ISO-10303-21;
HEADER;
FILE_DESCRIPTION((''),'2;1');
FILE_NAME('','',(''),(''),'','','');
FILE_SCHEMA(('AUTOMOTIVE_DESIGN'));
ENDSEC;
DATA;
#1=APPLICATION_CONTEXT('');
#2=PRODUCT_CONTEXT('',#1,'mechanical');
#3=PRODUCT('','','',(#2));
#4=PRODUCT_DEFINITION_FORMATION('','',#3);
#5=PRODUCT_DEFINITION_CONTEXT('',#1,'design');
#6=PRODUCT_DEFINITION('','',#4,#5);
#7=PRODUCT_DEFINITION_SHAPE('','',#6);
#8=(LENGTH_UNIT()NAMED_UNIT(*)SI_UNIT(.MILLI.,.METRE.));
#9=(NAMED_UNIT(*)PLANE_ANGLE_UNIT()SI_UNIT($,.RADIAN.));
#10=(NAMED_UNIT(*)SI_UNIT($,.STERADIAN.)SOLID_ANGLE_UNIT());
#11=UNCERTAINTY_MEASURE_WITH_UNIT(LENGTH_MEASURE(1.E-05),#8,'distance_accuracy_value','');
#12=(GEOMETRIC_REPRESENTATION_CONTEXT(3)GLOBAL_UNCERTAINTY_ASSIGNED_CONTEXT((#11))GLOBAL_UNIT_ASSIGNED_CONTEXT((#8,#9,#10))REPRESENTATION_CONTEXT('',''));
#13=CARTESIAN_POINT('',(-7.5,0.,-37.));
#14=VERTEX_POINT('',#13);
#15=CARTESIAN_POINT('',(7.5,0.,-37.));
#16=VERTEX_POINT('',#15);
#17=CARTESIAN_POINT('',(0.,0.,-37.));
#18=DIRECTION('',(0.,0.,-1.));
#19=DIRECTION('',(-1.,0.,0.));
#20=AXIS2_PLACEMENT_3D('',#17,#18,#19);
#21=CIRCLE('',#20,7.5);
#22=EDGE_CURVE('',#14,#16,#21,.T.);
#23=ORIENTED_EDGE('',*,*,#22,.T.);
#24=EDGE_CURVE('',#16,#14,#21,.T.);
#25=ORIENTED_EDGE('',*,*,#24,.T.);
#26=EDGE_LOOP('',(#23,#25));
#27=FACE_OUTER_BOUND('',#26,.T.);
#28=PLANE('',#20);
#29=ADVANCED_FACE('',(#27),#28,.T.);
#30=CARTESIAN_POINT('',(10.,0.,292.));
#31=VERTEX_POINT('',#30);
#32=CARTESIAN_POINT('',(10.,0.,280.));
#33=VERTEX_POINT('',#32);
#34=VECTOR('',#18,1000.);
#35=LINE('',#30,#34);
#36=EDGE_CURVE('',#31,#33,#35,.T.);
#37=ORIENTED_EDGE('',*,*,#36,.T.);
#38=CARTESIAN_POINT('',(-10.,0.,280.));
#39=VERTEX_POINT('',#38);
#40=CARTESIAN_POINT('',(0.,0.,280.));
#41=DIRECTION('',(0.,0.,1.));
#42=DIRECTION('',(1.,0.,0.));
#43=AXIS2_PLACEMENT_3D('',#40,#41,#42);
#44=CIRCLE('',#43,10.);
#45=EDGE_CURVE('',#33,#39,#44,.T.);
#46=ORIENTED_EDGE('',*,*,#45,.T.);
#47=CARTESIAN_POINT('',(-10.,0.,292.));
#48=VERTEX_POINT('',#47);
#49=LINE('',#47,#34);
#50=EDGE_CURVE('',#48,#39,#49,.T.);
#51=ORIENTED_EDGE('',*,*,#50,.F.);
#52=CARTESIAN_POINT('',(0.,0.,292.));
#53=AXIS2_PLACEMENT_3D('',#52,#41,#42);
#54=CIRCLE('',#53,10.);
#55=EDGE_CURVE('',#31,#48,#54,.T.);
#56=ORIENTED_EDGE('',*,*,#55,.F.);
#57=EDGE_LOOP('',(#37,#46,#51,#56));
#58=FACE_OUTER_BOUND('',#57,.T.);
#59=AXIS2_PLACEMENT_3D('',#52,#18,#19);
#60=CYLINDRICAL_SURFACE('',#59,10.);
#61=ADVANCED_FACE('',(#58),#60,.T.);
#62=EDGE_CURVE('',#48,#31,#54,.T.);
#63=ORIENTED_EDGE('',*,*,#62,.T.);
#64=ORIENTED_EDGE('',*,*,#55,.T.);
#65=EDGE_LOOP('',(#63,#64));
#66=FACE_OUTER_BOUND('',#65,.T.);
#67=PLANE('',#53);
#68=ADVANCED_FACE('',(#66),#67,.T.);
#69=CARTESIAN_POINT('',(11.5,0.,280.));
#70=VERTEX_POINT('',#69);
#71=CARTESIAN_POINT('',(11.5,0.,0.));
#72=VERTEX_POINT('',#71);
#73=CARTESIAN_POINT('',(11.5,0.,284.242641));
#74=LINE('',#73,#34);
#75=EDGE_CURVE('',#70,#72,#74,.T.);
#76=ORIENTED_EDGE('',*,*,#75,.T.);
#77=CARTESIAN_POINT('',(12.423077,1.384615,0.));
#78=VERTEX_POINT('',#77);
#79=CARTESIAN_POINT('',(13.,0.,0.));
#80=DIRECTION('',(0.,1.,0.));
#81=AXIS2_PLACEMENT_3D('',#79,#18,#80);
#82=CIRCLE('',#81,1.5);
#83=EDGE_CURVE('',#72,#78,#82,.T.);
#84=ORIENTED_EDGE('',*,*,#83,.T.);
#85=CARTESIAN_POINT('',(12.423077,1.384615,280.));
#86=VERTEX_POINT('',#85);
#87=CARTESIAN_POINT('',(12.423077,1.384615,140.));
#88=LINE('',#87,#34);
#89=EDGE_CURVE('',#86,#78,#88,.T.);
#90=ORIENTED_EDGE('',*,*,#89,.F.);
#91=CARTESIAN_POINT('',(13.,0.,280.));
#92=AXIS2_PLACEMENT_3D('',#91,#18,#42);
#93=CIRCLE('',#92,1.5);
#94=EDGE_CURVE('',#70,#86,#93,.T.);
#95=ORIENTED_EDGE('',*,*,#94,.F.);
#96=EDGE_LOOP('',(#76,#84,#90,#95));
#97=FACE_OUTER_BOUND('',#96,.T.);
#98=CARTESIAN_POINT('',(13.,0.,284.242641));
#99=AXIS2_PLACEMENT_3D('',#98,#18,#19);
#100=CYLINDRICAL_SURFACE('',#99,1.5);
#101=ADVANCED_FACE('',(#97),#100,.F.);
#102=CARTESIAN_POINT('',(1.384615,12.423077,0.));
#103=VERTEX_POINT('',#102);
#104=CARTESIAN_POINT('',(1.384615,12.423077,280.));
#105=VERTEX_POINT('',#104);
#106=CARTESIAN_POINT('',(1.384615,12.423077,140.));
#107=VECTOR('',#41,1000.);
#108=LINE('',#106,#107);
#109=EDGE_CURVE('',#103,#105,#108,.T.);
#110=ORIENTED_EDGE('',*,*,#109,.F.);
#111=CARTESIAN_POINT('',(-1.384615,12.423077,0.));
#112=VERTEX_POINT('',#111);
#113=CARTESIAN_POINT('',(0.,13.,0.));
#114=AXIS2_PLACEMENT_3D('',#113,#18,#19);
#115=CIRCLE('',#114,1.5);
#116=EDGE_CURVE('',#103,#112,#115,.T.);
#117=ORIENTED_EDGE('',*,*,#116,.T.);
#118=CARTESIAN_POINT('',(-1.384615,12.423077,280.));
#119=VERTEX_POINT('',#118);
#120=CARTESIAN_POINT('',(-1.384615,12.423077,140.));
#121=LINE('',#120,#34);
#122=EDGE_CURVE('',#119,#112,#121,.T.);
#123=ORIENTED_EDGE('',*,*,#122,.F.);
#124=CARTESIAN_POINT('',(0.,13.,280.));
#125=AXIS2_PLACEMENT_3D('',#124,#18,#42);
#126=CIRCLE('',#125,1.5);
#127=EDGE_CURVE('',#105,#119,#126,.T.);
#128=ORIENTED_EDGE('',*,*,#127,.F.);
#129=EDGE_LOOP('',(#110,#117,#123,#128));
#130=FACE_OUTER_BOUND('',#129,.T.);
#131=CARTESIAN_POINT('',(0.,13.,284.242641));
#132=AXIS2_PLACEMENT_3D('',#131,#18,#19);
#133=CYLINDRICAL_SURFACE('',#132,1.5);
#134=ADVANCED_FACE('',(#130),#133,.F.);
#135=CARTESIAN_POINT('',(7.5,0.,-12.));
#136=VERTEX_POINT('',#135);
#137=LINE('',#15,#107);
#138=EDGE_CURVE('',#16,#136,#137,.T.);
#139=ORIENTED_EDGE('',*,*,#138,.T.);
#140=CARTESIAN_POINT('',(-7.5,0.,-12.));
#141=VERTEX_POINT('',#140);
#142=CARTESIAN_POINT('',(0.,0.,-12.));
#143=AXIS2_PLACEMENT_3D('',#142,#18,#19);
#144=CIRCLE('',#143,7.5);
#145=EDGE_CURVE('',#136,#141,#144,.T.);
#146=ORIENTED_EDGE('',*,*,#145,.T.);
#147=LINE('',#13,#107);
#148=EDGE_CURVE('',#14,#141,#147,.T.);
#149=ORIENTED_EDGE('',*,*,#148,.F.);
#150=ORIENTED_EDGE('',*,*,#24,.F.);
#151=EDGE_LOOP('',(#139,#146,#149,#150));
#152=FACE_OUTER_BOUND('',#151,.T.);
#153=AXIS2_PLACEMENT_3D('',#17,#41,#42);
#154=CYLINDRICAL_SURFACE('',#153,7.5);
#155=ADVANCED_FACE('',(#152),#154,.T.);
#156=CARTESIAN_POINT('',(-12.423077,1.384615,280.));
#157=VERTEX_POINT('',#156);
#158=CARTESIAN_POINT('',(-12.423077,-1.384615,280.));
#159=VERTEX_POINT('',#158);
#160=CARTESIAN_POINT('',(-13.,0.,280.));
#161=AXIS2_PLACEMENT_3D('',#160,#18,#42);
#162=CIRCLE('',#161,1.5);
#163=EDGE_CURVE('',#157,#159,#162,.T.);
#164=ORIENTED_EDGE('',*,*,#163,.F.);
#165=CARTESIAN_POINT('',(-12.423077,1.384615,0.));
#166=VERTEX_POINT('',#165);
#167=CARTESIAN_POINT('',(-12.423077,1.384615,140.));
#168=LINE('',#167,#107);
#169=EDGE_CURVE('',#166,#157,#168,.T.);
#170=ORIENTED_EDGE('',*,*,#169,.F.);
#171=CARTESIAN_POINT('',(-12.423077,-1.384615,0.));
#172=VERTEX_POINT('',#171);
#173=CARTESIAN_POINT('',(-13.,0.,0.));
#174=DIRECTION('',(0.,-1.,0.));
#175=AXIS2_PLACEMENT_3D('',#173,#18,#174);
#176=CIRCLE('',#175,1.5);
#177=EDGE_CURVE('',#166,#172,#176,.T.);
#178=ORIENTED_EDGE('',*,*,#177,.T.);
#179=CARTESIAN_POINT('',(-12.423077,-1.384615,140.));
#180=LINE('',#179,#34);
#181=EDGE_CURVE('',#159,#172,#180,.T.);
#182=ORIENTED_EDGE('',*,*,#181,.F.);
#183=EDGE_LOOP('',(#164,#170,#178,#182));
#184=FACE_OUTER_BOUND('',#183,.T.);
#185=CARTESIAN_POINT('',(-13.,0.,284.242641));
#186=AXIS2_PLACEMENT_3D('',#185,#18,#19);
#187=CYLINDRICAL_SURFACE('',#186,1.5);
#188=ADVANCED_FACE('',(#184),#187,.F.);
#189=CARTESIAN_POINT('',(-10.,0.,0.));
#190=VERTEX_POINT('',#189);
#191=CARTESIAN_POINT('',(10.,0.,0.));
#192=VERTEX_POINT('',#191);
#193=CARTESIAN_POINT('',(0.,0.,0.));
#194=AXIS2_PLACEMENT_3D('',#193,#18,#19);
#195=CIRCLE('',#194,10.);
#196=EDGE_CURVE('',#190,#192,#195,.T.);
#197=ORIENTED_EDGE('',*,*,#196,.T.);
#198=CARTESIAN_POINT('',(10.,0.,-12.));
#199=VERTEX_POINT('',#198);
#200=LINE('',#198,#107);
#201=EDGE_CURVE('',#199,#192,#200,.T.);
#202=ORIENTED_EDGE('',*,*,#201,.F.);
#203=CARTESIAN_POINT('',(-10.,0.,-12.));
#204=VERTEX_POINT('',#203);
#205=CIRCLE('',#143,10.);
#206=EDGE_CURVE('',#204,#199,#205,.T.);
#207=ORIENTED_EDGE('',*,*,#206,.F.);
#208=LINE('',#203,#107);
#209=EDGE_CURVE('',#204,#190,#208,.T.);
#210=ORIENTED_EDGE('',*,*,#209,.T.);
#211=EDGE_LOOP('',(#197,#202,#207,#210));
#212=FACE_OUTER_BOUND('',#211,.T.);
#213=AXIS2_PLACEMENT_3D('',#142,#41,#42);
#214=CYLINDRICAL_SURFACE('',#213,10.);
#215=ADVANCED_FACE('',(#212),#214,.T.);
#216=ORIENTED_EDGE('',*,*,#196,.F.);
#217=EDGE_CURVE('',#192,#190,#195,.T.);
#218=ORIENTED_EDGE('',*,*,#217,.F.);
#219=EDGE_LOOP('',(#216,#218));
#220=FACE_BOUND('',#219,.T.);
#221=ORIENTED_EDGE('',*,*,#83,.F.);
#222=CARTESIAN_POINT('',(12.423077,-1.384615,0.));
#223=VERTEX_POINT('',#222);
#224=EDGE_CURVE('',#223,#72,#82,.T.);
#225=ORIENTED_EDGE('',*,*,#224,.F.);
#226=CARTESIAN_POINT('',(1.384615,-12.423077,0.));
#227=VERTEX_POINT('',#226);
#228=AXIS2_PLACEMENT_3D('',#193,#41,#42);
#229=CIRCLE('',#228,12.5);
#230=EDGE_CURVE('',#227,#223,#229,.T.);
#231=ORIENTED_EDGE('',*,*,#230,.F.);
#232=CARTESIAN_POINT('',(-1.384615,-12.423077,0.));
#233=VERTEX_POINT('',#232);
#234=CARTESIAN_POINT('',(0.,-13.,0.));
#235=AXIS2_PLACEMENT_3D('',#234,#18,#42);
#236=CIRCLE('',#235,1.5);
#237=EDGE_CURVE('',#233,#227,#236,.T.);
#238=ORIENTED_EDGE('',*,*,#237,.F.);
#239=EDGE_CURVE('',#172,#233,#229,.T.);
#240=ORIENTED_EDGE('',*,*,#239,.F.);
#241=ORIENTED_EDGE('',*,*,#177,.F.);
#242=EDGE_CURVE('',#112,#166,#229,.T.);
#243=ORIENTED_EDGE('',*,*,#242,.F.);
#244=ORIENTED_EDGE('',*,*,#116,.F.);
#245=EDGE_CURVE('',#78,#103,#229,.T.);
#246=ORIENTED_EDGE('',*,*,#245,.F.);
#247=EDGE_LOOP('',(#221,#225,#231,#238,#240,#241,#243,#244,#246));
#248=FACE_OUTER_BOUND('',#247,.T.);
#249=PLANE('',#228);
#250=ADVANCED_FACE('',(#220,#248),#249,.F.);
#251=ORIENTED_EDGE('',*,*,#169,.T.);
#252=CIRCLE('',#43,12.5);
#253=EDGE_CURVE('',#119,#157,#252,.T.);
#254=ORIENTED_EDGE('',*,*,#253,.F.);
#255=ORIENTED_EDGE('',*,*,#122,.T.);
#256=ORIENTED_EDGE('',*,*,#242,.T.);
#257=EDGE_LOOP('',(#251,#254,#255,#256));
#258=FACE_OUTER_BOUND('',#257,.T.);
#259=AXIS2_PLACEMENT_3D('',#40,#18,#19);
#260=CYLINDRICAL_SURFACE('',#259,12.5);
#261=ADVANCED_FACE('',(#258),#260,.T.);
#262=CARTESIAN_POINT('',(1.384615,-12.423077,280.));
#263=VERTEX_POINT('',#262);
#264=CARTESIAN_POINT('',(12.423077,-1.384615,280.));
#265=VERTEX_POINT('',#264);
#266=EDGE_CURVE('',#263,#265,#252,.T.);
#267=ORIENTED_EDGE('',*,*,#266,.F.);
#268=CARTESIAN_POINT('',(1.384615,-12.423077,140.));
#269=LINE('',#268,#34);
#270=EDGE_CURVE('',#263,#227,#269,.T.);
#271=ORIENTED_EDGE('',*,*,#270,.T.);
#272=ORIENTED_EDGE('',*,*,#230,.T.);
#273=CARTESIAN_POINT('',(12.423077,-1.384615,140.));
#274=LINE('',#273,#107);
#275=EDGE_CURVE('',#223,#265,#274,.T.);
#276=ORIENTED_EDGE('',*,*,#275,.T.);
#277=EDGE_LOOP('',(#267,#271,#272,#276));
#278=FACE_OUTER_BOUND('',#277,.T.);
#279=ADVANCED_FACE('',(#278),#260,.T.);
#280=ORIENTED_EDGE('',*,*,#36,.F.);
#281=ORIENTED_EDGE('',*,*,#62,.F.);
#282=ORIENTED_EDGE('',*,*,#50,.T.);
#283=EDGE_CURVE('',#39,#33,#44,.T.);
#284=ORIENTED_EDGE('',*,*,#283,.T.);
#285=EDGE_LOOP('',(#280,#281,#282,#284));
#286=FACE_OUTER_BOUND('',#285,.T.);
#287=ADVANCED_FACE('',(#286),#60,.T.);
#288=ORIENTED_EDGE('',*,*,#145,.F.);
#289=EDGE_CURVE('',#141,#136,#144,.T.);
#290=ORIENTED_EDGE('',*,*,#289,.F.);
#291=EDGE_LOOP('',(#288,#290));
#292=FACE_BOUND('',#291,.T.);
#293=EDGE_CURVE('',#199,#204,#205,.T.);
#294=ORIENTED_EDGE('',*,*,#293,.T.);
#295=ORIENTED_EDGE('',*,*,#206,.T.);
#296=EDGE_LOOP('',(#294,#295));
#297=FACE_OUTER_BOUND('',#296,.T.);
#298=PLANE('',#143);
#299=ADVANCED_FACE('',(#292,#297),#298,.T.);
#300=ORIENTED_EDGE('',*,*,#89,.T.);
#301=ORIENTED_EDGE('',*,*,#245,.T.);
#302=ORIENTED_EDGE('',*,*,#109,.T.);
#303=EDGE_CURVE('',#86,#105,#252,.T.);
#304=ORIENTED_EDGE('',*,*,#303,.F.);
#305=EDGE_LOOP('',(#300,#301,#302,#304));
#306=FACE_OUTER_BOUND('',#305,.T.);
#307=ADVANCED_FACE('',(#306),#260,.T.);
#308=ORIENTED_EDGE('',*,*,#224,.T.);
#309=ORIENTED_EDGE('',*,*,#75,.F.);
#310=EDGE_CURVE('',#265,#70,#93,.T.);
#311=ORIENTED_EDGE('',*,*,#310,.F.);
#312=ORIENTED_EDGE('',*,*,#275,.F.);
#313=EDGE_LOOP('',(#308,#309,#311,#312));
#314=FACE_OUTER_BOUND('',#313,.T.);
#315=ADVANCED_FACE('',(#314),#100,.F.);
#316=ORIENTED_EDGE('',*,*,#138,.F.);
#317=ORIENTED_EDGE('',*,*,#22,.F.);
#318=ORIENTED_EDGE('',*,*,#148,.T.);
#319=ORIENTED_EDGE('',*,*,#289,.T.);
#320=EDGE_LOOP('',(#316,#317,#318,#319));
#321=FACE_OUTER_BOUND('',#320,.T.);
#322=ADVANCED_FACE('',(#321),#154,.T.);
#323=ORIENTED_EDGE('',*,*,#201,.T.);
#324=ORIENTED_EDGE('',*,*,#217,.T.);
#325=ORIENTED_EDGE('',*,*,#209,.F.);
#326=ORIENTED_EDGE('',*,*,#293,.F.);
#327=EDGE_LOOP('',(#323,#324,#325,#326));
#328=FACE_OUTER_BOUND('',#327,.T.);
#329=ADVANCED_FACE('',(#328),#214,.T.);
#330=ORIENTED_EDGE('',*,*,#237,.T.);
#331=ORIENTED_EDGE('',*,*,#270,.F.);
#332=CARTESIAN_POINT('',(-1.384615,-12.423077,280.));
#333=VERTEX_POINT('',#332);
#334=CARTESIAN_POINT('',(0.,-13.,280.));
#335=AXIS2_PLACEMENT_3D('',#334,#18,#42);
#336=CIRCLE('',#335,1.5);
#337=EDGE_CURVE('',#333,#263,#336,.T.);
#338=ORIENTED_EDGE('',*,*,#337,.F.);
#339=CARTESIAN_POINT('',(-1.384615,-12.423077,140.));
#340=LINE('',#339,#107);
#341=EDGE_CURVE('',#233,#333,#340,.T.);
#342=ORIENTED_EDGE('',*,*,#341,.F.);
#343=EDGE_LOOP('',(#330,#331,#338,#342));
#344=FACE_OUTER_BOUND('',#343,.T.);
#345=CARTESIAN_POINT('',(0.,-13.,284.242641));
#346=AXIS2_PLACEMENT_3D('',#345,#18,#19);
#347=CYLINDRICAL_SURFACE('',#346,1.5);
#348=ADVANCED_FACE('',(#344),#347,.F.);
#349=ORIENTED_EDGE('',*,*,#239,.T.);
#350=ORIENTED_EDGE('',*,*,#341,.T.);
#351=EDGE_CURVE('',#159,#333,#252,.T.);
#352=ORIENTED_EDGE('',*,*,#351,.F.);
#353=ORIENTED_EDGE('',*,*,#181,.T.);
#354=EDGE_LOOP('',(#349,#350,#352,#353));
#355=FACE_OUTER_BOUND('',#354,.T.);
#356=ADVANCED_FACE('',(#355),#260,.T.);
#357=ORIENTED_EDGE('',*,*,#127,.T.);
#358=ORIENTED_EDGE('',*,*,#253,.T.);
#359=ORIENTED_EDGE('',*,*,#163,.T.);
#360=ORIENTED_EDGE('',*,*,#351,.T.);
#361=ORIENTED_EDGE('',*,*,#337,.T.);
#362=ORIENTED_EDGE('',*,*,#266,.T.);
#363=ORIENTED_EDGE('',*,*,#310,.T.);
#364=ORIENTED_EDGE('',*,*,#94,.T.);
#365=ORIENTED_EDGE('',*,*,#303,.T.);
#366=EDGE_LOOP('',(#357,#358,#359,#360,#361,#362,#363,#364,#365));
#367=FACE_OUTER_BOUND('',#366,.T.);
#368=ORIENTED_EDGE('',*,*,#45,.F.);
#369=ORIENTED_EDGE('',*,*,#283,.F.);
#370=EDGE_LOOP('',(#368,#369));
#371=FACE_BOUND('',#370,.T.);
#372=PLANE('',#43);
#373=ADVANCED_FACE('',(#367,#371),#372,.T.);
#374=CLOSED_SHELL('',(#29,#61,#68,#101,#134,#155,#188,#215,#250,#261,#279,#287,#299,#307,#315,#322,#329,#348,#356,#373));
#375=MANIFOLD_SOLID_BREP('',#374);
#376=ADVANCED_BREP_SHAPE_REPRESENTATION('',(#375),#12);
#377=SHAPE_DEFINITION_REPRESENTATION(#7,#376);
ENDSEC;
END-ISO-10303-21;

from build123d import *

# Parameters (mm, degrees)
SKETCH_1_R               = 12.5
EXTRUDE_1_DEPTH          = 280
SKETCH_2_R               = 10
EXTRUDE_2_DEPTH          = 12
EXTRUDE_START            = 12
SKETCH_3_R               = 10
EXTRUDE_3_DEPTH          = 12
SKETCH_4_R               = 7.5
EXTRUDE_4_DEPTH          = 25
SKETCH_5_R               = 1.5
CUT_EXTRUDE_1_DEPTH      = 280
PATTERN_CIRCULAR_1_COUNT = 4


with BuildPart() as part:
    # 草图1 → 凸台-拉伸1 (new body)
    with BuildSketch(Plane.XY):
        Circle(SKETCH_1_R)
    extrude(amount=EXTRUDE_1_DEPTH)

    # 草图2 → 凸台-拉伸2 (add)
    with BuildSketch(Plane.XY.offset(280)):
        Circle(SKETCH_2_R)
    extrude(amount=EXTRUDE_2_DEPTH)

    # 草图3 → 凸台-拉伸3 (add)
    with BuildSketch(Plane(origin=(0, 0, 0), x_dir=(-1, 0, 0), z_dir=(0, 0, -1)).offset(EXTRUDE_START)):
        with Locations(Location((0, 0, 0), (0, 0, 180))):
            Circle(SKETCH_3_R)
    extrude(amount=-EXTRUDE_3_DEPTH)

    # 草图4 → 凸台-拉伸4 (add)
    with BuildSketch(Plane(origin=(0, 0, -12), x_dir=(-1, 0, 0), z_dir=(0, 0, -1))):
        Circle(SKETCH_4_R)
    extrude(amount=EXTRUDE_4_DEPTH)

    # 草图5 → 切除-拉伸1 (cut)
    with BuildSketch(Plane(origin=(0, 0, 0), x_dir=(-1, 0, 0), z_dir=(0, 0, -1))):
        with Locations((0, 13)):
            Circle(SKETCH_5_R)
    cut_extrude_1 = extrude(amount=-CUT_EXTRUDE_1_DEPTH, mode=Mode.SUBTRACT)

    # 阵列(圆周)1: 切除-拉伸1 ×4 about axis
    pattern_circular_1_axis = Axis((0, 0, 0), (0, 0, 1))
    for i in range(1, PATTERN_CIRCULAR_1_COUNT):
        add(cut_extrude_1.rotate(pattern_circular_1_axis, i * 360 / PATTERN_CIRCULAR_1_COUNT), mode=Mode.SUBTRACT)


solid = part.part
